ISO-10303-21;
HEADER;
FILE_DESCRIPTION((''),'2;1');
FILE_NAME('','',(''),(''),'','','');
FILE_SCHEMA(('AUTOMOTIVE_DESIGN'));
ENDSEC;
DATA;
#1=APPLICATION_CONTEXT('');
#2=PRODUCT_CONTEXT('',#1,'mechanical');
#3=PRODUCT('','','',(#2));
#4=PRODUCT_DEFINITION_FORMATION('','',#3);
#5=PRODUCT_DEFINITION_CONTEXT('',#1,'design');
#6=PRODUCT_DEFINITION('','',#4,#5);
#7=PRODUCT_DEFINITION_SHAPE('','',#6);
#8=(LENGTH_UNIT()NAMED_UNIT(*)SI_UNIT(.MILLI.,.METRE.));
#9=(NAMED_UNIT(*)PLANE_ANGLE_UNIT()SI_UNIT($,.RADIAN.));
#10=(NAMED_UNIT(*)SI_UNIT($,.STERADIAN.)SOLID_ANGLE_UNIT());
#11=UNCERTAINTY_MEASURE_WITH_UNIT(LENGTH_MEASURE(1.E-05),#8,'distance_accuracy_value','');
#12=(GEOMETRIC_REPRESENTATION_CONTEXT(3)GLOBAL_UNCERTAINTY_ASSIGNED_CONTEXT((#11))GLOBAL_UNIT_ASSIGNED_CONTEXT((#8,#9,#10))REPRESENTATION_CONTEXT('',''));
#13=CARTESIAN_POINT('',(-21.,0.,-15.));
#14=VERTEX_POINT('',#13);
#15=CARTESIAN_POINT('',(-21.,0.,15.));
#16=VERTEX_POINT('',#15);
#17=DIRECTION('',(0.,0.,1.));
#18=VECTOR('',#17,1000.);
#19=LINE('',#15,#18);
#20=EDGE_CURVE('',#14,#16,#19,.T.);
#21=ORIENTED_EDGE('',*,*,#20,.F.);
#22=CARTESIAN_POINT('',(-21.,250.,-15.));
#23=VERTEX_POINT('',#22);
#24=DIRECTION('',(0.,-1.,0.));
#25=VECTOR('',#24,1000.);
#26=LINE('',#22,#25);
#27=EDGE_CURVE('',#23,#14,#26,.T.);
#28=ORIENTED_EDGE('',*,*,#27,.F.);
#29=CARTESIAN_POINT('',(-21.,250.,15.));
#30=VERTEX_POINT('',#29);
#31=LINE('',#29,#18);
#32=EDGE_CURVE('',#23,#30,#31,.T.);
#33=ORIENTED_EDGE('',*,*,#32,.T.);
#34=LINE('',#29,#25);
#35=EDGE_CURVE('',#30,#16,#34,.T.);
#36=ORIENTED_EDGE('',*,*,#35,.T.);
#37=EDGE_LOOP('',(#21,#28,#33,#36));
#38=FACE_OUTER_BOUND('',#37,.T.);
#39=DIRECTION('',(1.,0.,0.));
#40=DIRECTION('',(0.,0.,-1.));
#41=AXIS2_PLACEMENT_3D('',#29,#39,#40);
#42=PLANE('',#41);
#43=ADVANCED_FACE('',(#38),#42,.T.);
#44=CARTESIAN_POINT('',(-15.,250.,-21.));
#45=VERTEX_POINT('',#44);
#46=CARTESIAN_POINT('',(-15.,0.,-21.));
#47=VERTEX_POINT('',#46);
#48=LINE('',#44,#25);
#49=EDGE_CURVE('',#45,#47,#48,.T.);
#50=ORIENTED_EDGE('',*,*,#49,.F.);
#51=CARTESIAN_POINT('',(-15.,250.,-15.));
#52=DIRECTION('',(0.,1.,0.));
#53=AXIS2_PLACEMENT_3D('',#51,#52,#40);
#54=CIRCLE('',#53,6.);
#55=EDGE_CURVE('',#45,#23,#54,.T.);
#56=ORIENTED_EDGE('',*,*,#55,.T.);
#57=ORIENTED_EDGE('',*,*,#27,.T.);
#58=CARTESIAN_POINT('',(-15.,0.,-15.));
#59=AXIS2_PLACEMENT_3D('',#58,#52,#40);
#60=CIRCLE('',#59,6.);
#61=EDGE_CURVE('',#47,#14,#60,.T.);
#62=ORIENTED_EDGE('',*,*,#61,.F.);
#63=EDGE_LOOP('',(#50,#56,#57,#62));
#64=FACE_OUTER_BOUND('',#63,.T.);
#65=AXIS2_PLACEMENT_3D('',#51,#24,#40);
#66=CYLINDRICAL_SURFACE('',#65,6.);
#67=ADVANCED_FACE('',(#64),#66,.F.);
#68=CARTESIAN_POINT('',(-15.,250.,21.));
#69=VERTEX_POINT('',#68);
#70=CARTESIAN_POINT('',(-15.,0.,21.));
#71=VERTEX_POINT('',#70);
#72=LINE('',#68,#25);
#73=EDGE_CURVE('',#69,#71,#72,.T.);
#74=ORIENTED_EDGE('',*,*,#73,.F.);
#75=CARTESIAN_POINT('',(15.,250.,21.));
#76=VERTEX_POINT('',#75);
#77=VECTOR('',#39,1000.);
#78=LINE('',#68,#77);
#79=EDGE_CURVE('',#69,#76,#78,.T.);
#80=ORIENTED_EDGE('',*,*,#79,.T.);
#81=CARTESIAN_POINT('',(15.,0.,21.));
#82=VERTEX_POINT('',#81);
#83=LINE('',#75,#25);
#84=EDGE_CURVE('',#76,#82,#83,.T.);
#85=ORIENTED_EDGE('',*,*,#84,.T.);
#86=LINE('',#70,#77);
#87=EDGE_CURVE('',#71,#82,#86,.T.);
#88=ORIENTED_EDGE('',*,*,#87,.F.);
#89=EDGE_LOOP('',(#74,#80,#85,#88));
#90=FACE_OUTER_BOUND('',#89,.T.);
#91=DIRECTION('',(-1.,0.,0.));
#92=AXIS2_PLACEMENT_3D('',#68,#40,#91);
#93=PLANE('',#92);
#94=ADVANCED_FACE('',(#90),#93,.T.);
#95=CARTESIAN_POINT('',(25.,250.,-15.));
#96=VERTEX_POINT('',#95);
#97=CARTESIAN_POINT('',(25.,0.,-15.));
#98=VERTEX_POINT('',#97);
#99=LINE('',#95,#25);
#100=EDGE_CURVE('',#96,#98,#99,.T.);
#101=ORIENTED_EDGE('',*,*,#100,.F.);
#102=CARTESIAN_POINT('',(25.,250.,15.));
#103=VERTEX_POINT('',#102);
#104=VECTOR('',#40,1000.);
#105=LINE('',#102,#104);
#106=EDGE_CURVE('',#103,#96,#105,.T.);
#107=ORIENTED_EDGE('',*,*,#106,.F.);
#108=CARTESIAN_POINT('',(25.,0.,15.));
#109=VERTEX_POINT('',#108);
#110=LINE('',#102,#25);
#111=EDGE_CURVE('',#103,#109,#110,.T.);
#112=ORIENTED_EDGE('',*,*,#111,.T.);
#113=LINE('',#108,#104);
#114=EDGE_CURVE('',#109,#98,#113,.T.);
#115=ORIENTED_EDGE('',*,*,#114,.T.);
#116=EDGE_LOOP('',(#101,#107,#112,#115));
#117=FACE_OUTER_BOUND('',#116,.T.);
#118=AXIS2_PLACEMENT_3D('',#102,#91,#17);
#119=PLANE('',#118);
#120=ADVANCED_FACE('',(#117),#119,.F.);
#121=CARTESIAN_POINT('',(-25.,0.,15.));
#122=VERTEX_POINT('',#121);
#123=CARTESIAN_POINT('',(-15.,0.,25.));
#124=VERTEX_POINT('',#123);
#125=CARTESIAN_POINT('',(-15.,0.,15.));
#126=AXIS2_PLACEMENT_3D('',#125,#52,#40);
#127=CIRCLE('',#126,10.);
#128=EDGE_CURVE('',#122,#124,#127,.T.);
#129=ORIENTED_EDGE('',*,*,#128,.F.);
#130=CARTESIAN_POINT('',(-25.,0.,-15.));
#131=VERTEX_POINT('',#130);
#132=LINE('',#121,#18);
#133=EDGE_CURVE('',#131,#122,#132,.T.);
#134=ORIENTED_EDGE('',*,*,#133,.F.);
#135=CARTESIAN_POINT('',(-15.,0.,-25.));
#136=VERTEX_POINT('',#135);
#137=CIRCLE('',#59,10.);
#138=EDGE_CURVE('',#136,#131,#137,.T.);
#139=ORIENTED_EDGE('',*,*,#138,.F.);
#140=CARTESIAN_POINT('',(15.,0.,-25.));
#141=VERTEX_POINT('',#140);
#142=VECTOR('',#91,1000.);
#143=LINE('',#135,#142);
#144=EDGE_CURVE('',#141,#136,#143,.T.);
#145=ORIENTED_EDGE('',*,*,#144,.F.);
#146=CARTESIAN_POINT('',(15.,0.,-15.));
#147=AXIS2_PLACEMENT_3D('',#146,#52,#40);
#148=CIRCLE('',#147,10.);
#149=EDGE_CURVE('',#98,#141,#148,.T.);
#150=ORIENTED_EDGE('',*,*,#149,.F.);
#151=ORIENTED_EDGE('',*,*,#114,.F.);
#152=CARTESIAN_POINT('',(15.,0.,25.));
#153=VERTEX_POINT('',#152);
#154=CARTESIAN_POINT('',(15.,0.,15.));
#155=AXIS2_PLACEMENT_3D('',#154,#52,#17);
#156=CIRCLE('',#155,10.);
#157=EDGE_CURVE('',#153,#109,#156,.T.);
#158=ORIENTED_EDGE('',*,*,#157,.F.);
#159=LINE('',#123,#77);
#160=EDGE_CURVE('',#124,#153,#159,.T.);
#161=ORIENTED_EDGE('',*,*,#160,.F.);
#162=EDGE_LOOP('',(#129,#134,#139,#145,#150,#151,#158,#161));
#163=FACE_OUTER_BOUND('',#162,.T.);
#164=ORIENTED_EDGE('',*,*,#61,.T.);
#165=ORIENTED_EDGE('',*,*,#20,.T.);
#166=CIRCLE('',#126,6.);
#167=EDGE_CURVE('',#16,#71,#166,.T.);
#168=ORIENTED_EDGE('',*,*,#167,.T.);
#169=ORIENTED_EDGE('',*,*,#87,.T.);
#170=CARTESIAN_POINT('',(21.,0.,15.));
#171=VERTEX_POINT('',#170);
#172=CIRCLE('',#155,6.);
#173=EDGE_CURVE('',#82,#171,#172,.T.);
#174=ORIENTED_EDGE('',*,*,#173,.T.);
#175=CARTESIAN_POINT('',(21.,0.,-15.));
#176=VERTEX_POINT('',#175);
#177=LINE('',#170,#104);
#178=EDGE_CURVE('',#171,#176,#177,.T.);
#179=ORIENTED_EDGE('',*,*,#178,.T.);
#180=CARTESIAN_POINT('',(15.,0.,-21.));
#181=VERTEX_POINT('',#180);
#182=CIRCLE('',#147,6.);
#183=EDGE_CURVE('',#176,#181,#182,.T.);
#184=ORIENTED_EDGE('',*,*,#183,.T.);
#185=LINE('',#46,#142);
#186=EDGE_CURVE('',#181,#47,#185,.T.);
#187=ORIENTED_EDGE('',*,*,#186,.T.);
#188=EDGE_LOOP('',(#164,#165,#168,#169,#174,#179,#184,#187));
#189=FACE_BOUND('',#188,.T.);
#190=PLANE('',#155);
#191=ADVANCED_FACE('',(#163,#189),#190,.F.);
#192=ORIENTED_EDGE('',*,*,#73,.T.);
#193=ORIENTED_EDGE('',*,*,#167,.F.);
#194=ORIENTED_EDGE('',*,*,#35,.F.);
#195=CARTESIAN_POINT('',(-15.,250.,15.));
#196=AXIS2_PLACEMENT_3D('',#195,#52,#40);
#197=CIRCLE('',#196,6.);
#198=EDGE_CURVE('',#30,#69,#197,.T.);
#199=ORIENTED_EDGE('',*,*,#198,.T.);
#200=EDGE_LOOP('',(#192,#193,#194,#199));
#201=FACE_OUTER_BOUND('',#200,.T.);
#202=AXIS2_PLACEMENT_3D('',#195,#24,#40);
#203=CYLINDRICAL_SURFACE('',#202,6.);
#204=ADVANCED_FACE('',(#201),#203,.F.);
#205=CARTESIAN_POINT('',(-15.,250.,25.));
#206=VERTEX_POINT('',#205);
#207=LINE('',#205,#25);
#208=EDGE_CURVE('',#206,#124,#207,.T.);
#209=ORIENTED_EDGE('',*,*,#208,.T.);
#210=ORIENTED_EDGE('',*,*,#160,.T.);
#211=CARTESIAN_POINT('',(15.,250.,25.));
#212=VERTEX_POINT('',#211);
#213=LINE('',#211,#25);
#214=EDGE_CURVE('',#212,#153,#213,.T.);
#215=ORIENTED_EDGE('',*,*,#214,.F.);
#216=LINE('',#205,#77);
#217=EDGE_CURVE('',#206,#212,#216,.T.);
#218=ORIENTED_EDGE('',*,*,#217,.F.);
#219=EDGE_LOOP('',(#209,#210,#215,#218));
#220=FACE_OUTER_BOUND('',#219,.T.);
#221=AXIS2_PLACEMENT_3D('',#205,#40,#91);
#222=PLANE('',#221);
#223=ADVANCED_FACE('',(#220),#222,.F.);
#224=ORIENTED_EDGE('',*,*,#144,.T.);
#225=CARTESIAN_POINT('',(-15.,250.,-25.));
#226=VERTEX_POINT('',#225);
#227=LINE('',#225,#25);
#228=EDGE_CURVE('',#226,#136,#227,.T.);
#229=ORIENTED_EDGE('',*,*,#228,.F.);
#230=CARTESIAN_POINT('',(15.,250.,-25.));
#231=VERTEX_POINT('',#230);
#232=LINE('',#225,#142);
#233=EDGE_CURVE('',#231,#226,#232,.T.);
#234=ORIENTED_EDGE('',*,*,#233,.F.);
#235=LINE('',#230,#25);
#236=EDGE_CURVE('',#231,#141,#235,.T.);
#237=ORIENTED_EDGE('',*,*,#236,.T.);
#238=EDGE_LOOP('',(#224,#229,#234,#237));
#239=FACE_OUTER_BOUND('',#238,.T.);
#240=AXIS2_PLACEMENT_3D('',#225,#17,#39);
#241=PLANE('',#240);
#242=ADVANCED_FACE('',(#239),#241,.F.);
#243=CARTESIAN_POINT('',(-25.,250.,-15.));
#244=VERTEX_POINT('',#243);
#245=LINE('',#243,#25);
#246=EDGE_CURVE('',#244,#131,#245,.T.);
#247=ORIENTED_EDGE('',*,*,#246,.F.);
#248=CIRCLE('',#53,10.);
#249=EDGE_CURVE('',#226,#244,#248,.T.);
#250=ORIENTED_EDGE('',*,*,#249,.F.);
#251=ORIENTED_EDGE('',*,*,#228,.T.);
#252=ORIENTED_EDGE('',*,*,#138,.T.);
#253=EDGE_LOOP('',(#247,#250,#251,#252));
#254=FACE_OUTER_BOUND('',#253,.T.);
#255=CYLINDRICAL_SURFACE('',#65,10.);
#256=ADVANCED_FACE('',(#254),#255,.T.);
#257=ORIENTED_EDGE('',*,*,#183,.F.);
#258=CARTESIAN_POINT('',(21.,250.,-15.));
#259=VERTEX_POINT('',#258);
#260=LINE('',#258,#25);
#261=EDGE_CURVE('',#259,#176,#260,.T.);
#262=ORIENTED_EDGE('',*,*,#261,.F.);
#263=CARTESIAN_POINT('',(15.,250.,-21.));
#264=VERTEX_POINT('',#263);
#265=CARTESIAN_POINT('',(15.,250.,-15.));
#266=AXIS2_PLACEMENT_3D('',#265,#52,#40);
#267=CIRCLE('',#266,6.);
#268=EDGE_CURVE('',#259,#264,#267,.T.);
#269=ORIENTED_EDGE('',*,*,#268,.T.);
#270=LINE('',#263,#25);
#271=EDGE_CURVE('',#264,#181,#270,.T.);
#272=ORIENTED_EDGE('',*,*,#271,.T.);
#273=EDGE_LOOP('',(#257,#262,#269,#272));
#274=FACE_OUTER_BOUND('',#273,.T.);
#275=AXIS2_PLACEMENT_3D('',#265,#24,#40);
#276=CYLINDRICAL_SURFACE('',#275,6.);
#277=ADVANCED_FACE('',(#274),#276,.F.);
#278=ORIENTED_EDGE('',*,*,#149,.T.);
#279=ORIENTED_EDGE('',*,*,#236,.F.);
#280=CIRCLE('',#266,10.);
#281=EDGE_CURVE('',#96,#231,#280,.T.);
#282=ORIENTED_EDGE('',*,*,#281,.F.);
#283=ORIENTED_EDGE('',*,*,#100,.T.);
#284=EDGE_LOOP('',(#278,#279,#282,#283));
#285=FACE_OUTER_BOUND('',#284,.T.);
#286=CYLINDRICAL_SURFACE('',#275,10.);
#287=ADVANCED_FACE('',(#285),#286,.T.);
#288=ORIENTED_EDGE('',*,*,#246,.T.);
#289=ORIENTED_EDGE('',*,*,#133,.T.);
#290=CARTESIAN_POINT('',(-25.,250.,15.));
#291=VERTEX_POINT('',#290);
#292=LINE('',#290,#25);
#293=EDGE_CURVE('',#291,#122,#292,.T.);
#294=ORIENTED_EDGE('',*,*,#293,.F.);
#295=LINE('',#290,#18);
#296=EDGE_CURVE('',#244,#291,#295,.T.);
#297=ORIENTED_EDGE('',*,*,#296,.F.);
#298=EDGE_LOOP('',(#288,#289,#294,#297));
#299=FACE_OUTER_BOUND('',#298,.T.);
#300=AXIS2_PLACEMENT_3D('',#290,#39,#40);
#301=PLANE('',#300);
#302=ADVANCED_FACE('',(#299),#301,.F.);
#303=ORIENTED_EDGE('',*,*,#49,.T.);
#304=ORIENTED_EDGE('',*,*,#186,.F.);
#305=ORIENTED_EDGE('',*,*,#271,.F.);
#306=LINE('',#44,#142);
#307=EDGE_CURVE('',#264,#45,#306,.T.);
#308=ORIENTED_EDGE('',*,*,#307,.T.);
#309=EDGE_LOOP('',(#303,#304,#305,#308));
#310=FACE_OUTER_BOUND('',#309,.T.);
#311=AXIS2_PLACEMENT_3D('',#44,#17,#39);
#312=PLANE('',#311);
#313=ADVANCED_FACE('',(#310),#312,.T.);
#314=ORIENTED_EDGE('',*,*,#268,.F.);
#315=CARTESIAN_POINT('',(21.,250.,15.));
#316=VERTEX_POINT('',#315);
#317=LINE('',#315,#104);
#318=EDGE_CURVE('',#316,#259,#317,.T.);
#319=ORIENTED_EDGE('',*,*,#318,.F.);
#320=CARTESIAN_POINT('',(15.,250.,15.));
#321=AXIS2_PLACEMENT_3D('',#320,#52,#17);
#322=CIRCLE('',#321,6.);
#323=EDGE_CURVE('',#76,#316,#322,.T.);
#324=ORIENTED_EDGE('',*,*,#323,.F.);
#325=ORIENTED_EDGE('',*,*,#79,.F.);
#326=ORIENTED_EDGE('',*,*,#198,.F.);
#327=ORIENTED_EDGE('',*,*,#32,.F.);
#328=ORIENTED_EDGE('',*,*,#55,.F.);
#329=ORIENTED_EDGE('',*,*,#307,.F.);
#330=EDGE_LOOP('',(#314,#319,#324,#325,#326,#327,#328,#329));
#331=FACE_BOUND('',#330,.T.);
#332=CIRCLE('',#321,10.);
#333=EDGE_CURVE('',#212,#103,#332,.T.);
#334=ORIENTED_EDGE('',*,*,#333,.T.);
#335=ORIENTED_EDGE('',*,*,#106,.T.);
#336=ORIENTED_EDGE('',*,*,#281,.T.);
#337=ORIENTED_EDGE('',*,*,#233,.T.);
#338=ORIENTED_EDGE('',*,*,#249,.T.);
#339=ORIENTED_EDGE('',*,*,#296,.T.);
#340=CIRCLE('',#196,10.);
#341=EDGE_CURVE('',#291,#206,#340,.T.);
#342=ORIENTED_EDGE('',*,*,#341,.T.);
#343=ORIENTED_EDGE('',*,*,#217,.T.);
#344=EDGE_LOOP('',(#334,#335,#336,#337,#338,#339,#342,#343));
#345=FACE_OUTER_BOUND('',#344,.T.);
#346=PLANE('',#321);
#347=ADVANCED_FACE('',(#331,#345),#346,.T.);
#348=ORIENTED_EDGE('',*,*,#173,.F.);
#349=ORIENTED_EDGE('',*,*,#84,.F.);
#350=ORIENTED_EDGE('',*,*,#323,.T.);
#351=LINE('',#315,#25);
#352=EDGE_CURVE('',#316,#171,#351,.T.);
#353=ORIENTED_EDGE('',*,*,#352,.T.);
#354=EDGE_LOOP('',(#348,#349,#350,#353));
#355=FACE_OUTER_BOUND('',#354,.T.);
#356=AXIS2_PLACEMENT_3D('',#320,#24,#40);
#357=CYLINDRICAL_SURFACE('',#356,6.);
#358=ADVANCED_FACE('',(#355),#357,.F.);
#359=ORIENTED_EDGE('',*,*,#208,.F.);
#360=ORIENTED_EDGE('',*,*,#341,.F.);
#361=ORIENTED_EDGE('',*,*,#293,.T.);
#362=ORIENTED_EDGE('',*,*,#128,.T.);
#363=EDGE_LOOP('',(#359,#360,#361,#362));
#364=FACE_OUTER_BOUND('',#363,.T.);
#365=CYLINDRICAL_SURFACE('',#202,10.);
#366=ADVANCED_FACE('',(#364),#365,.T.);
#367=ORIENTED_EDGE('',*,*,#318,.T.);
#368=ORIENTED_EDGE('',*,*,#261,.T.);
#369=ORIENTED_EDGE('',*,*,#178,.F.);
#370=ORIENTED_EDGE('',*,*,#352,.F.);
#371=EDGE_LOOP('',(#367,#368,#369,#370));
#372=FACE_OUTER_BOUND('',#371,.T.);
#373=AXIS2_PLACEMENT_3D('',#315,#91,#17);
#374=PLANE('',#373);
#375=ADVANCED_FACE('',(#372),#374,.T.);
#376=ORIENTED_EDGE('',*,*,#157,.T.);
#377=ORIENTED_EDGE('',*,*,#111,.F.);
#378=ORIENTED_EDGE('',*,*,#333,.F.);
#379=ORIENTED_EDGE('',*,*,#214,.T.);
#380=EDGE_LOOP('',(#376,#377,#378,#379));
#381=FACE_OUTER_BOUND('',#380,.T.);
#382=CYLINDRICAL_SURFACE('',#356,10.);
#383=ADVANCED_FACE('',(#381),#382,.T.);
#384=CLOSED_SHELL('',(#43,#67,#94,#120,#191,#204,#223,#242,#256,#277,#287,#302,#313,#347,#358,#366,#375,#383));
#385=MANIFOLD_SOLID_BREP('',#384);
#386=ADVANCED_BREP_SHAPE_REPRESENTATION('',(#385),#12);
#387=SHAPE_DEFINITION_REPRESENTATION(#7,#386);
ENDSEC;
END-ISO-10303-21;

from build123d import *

# Parameters (mm, degrees)
BOSS_EXTRUDE1_DEPTH = 250


with BuildPart() as part:
    # Sketch1 → Boss-Extrude1 (new body)
    with BuildSketch(Plane(origin=(0, 0, 0), x_dir=(1, 0, 0), z_dir=(0, 1, 0))):
        with BuildLine():
            Line((-15, -25), (15, -25))
            ThreePointArc((15, -25), (22.071067812, -22.071067812), (25, -15))
            Line((25, -15), (25, 15))
            ThreePointArc((25, 15), (22.071067812, 22.071067812), (15, 25))
            Line((15, 25), (-15, 25))
            ThreePointArc((-15, 25), (-22.071067812, 22.071067812), (-25, 15))
            Line((-25, 15), (-25, -15))
            ThreePointArc((-25, -15), (-22.071067812, -22.071067812), (-15, -25))
        make_face()
        with BuildLine():
            Line((-15, 21), (15, 21))
            ThreePointArc((15, 21), (19.242640687, 19.242640687), (21, 15))
            Line((21, 15), (21, -15))
            ThreePointArc((21, -15), (19.242640687, -19.242640687), (15, -21))
            Line((15, -21), (-15, -21))
            ThreePointArc((-15, -21), (-19.242640687, -19.242640687), (-21, -15))
            Line((-21, -15), (-21, 15))
            ThreePointArc((-21, 15), (-19.242640687, 19.242640687), (-15, 21))
        make_face(mode=Mode.SUBTRACT)
    extrude(amount=BOSS_EXTRUDE1_DEPTH)


solid = part.part
